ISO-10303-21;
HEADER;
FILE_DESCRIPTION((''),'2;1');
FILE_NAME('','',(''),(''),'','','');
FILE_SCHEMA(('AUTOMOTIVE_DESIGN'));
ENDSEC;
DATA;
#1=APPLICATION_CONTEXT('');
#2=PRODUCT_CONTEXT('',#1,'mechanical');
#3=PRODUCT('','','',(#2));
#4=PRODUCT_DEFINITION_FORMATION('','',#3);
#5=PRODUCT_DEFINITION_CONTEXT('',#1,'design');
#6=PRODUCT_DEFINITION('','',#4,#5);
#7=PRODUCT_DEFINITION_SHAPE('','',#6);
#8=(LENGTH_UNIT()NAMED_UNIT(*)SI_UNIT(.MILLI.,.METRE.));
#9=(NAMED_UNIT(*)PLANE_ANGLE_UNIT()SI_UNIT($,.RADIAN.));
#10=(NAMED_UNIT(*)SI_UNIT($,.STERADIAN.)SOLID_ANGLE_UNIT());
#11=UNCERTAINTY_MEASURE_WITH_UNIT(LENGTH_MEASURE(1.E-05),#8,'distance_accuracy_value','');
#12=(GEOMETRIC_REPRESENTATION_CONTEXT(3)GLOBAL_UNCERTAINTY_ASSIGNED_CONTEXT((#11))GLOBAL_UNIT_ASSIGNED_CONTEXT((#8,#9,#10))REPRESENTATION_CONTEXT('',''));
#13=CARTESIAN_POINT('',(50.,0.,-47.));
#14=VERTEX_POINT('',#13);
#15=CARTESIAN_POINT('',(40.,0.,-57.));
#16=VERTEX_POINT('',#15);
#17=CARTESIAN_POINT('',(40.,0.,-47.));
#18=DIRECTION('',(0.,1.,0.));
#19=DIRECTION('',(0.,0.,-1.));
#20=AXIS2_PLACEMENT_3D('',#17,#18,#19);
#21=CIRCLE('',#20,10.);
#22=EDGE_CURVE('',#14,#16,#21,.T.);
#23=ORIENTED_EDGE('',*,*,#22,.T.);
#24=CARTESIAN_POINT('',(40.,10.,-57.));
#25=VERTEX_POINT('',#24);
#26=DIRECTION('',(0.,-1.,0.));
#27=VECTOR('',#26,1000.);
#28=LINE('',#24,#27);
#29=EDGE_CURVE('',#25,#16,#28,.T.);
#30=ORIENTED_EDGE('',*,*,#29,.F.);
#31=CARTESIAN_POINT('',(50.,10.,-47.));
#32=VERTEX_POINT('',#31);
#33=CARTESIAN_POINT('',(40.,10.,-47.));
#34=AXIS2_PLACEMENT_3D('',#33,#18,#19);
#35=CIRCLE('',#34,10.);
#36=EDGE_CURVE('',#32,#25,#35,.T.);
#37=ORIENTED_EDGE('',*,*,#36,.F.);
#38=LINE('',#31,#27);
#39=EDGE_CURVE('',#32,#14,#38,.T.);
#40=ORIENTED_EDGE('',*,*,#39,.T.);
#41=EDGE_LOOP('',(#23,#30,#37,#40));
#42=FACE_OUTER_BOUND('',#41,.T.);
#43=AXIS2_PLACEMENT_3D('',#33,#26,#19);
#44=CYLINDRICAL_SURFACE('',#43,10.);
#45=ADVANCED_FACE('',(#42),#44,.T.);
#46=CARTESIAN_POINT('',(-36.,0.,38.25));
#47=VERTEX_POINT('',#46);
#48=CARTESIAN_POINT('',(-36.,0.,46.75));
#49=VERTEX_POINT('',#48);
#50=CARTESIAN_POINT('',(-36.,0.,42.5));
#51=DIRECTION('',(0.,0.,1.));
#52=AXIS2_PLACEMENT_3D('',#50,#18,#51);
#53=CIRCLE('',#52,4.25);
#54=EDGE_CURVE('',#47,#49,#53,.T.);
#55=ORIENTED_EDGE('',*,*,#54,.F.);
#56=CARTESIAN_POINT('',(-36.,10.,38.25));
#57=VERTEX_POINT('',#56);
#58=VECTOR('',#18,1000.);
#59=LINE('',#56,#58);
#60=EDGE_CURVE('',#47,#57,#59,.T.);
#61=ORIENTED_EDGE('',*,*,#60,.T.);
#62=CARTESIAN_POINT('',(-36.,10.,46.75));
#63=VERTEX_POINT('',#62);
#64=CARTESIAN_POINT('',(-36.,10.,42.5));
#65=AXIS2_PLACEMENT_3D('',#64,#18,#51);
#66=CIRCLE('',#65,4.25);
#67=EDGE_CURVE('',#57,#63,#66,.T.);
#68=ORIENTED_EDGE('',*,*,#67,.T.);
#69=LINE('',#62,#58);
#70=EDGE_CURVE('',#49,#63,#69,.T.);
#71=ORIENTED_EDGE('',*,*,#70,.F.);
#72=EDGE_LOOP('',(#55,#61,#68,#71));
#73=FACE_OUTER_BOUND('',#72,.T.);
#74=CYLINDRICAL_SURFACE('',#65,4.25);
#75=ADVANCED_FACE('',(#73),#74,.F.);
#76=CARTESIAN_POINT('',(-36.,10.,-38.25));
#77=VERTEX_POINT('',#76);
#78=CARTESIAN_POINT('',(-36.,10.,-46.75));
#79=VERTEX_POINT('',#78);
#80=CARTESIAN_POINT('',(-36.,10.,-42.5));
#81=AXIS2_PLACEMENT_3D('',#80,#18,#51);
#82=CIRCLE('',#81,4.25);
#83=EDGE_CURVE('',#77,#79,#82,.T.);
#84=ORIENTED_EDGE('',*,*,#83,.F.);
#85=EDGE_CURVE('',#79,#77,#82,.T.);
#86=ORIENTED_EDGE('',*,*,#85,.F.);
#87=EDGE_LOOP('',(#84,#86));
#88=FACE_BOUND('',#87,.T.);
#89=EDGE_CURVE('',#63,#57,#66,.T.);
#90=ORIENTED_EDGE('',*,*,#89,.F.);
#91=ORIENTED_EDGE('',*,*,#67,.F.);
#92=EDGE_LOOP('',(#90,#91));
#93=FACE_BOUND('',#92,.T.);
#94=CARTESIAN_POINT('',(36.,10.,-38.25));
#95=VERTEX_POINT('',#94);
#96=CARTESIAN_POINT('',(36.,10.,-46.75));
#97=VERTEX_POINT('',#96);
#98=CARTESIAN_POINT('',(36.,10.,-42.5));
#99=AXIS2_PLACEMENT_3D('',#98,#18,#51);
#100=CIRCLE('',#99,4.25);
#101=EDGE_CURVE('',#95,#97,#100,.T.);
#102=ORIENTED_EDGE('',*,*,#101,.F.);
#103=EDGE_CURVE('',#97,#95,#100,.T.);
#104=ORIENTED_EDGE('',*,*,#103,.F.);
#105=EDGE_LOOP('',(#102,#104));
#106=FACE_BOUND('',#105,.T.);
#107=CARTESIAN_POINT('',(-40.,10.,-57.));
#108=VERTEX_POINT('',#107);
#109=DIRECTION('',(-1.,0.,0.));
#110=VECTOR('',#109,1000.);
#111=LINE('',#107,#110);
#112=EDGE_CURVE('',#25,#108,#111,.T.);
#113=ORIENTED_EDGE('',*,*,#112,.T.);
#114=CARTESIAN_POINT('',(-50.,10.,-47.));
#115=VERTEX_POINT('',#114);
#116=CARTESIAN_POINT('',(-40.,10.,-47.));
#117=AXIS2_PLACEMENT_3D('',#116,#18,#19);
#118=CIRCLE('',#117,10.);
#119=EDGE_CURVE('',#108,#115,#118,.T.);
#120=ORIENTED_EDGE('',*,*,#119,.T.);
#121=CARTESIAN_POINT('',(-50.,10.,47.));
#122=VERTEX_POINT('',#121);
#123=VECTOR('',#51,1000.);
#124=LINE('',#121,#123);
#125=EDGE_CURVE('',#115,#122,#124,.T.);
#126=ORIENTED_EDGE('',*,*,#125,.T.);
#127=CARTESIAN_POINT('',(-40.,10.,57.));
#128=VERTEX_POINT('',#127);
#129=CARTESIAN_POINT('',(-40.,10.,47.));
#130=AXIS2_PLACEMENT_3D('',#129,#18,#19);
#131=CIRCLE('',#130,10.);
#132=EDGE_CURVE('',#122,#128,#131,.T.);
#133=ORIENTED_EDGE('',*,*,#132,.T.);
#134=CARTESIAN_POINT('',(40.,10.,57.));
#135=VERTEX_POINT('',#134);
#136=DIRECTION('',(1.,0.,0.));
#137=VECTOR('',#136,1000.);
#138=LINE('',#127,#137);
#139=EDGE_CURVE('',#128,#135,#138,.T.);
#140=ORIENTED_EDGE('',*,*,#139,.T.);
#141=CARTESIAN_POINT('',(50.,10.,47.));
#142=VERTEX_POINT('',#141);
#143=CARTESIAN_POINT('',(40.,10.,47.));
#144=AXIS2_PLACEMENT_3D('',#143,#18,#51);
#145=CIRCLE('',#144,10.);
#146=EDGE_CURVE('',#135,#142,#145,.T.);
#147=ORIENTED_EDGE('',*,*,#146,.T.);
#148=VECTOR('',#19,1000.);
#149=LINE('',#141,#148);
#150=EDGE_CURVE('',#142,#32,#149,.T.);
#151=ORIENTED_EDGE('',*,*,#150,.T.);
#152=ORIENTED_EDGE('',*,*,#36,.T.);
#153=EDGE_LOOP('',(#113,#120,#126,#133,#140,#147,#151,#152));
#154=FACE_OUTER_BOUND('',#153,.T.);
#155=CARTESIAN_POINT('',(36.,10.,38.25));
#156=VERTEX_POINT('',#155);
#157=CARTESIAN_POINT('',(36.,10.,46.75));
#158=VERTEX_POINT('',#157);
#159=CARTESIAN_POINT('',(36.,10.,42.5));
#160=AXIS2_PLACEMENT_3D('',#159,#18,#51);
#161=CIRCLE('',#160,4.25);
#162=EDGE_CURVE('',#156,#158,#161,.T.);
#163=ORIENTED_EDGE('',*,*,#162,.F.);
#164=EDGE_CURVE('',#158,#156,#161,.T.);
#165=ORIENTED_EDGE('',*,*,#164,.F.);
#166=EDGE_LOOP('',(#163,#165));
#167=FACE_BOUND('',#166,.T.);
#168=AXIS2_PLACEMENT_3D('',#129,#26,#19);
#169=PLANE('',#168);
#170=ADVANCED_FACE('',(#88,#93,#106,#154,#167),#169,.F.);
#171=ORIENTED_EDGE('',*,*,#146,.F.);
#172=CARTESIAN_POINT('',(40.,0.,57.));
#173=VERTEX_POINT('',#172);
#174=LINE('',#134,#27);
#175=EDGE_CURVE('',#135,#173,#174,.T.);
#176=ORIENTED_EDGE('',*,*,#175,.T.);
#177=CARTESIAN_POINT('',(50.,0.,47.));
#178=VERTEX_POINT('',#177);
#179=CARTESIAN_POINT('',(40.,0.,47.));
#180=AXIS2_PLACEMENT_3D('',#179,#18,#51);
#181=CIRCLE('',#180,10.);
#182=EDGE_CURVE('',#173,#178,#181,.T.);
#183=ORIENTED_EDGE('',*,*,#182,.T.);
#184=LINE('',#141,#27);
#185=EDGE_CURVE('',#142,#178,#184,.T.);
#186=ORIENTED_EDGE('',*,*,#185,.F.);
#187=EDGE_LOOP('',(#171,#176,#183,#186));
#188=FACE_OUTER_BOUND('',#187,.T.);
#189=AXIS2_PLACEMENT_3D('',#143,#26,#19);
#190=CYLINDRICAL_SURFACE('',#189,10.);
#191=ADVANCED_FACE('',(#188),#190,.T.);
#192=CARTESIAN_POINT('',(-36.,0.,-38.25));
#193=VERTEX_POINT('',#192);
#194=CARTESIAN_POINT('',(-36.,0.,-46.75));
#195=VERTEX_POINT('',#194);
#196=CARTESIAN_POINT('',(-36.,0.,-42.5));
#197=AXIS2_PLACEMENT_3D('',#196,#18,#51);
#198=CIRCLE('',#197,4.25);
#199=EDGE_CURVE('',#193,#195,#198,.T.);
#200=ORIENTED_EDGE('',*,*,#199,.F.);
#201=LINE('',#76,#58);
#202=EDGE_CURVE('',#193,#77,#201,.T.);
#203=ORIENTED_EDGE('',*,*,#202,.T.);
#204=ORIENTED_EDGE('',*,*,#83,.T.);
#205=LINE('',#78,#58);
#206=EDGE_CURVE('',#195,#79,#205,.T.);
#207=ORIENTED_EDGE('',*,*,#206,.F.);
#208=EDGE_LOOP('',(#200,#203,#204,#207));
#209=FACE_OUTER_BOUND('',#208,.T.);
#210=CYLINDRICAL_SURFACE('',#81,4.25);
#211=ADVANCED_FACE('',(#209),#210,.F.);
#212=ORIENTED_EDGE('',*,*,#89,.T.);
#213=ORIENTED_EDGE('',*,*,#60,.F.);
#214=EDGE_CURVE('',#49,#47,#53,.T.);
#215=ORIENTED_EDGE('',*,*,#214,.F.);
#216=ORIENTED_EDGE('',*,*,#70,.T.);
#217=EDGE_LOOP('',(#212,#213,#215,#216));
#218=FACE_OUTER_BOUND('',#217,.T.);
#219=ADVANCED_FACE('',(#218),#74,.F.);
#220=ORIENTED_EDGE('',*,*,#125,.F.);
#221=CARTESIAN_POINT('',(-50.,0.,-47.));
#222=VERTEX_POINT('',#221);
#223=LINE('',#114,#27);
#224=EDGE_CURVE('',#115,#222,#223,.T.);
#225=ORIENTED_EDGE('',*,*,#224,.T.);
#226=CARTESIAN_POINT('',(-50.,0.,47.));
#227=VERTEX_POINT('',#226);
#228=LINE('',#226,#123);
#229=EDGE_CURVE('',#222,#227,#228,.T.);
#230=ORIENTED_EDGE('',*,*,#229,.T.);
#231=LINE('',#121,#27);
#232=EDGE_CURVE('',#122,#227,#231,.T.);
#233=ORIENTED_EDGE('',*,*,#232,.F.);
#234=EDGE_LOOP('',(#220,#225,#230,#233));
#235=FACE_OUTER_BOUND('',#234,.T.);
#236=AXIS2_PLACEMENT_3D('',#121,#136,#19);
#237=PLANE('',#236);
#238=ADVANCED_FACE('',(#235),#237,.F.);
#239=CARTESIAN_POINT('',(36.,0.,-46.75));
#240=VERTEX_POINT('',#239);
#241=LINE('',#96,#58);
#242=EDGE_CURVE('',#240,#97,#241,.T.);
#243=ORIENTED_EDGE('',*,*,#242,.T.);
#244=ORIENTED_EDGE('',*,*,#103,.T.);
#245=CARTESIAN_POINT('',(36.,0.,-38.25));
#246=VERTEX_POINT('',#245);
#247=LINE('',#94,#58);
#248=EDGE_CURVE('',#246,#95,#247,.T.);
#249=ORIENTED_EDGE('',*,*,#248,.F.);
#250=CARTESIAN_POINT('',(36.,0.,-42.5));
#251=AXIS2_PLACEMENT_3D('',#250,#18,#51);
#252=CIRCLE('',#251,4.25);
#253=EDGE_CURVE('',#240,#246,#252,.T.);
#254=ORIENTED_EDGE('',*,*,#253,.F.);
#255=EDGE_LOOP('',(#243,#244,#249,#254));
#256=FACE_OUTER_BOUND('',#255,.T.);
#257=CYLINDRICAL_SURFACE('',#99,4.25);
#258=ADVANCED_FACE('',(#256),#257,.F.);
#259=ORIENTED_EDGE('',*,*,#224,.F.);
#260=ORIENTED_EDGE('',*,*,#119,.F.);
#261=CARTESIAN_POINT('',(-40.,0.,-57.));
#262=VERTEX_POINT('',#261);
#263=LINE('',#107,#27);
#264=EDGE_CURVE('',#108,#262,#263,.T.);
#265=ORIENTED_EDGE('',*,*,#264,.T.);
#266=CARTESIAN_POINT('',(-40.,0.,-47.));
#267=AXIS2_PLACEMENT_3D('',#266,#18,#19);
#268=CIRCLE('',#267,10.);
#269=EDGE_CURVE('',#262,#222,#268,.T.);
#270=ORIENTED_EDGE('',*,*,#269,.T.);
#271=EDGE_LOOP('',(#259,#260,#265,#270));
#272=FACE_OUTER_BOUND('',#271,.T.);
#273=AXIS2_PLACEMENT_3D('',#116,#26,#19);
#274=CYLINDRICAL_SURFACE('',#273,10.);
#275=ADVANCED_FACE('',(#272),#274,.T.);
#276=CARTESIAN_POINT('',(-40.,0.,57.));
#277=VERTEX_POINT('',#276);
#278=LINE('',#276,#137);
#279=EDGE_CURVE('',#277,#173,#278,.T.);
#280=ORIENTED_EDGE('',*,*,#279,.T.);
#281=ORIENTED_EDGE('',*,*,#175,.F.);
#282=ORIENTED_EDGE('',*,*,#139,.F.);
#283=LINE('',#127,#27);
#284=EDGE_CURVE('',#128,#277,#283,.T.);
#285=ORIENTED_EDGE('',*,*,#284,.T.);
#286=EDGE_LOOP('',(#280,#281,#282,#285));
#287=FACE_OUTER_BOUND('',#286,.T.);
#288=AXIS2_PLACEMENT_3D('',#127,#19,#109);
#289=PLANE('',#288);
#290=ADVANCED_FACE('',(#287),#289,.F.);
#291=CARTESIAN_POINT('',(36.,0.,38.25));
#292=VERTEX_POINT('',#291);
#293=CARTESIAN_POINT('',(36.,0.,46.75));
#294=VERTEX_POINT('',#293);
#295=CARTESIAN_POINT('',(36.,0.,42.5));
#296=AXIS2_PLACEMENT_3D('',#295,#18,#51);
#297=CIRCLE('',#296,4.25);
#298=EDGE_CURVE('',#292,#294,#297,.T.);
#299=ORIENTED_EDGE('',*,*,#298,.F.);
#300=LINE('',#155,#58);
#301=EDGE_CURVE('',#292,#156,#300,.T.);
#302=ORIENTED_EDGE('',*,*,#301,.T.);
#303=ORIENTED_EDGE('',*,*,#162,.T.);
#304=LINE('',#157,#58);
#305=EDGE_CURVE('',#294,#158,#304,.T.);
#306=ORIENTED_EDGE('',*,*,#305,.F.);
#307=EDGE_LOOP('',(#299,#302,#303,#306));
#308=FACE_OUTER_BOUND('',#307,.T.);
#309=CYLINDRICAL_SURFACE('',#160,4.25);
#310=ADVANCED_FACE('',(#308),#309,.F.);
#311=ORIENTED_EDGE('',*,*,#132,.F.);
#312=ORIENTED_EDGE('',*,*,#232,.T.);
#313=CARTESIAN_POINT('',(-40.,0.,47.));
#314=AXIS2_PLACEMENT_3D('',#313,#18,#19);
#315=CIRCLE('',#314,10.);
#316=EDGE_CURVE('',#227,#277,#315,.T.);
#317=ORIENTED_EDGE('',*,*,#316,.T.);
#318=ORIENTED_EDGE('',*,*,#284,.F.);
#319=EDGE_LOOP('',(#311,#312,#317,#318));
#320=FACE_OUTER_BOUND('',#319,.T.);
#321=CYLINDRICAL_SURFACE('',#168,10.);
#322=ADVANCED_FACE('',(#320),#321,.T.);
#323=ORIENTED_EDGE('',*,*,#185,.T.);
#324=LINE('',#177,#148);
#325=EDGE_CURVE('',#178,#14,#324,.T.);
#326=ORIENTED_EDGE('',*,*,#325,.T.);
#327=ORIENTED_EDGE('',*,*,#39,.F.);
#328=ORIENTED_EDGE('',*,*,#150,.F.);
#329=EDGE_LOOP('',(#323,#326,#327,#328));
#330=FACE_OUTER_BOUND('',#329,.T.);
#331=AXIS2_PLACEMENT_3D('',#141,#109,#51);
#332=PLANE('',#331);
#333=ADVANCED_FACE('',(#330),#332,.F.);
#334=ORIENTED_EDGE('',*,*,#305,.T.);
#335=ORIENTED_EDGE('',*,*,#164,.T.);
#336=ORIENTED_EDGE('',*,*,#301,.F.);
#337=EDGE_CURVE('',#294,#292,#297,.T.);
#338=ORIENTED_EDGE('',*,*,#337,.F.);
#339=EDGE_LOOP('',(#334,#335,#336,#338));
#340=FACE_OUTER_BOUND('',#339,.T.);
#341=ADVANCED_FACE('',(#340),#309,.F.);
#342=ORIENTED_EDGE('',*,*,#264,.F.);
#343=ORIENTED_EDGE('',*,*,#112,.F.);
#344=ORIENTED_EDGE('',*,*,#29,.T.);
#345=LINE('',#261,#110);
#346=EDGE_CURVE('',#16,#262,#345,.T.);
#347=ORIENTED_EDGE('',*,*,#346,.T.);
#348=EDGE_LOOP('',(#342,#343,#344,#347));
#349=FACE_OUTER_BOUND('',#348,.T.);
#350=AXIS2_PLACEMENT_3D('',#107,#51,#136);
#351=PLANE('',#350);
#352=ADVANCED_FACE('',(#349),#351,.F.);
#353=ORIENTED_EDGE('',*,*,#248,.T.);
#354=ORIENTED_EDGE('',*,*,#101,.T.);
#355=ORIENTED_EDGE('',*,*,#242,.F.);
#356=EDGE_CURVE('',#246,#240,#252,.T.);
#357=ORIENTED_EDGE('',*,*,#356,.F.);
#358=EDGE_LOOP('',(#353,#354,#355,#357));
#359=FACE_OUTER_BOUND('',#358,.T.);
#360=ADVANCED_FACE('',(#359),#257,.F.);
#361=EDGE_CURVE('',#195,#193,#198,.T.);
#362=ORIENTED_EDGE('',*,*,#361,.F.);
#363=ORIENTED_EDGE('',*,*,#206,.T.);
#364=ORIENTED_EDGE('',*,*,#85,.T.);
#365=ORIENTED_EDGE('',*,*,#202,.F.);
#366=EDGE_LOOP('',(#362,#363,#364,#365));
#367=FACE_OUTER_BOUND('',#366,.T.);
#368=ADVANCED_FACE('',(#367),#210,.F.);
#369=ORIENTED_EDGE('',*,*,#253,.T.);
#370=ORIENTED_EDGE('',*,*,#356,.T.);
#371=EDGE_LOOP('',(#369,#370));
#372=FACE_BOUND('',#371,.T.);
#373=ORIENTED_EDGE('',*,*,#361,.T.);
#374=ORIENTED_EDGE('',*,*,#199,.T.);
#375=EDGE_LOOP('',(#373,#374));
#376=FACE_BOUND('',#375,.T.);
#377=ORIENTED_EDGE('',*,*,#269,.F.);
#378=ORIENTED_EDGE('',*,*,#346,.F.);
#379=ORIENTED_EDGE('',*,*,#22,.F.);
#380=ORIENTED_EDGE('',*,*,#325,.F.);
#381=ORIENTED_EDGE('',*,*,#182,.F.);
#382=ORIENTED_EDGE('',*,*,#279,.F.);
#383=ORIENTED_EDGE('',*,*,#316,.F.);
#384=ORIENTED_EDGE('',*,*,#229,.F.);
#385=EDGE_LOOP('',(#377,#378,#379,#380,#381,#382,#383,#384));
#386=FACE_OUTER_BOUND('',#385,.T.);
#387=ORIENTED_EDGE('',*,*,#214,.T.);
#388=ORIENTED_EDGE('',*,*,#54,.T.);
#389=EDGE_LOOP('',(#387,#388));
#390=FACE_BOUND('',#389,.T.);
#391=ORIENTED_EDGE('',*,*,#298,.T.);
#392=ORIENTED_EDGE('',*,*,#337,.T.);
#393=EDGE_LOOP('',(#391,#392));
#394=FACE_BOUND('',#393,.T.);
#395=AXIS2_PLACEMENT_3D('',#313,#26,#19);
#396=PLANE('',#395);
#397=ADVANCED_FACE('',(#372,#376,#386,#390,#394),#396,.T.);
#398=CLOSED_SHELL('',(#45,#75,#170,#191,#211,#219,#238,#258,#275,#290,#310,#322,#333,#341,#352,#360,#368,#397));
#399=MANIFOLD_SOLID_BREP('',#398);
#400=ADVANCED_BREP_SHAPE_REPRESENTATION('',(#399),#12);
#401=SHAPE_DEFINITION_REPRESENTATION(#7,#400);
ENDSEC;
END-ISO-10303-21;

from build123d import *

# Parameters (mm, degrees)
BOSS_EXTRUDE1_DEPTH = 10
M10_TAPPED_HOLE1_D  = 8.5


with BuildPart() as part:
    # Sketch1 → Boss-Extrude1 (new body)
    with BuildSketch(Plane(origin=(0, 0, 0), x_dir=(1, 0, 0), z_dir=(0, 1, 0))):
        with BuildLine():
            Line((-40, -57), (40, -57))
            ThreePointArc((40, -57), (47.071067812, -54.071067812), (50, -47))
            Line((50, -47), (50, 47))
            ThreePointArc((50, 47), (47.071067812, 54.071067812), (40, 57))
            Line((40, 57), (-40, 57))
            ThreePointArc((-40, 57), (-47.071067812, 54.071067812), (-50, 47))
            Line((-50, 47), (-50, -47))
            ThreePointArc((-50, -47), (-47.071067812, -54.071067812), (-40, -57))
        make_face()
    extrude(amount=BOSS_EXTRUDE1_DEPTH)

    # M10 Tapped Hole1 (through all)
    with Locations(Plane(origin=(0, 10, 0), x_dir=(1, 0, 0), z_dir=(0, 1, 0))):
        with Locations((36, 42.5), (-36, -42.5), (-36, 42.5), (36, -42.5)):
            Hole(M10_TAPPED_HOLE1_D / 2)


solid = part.part
